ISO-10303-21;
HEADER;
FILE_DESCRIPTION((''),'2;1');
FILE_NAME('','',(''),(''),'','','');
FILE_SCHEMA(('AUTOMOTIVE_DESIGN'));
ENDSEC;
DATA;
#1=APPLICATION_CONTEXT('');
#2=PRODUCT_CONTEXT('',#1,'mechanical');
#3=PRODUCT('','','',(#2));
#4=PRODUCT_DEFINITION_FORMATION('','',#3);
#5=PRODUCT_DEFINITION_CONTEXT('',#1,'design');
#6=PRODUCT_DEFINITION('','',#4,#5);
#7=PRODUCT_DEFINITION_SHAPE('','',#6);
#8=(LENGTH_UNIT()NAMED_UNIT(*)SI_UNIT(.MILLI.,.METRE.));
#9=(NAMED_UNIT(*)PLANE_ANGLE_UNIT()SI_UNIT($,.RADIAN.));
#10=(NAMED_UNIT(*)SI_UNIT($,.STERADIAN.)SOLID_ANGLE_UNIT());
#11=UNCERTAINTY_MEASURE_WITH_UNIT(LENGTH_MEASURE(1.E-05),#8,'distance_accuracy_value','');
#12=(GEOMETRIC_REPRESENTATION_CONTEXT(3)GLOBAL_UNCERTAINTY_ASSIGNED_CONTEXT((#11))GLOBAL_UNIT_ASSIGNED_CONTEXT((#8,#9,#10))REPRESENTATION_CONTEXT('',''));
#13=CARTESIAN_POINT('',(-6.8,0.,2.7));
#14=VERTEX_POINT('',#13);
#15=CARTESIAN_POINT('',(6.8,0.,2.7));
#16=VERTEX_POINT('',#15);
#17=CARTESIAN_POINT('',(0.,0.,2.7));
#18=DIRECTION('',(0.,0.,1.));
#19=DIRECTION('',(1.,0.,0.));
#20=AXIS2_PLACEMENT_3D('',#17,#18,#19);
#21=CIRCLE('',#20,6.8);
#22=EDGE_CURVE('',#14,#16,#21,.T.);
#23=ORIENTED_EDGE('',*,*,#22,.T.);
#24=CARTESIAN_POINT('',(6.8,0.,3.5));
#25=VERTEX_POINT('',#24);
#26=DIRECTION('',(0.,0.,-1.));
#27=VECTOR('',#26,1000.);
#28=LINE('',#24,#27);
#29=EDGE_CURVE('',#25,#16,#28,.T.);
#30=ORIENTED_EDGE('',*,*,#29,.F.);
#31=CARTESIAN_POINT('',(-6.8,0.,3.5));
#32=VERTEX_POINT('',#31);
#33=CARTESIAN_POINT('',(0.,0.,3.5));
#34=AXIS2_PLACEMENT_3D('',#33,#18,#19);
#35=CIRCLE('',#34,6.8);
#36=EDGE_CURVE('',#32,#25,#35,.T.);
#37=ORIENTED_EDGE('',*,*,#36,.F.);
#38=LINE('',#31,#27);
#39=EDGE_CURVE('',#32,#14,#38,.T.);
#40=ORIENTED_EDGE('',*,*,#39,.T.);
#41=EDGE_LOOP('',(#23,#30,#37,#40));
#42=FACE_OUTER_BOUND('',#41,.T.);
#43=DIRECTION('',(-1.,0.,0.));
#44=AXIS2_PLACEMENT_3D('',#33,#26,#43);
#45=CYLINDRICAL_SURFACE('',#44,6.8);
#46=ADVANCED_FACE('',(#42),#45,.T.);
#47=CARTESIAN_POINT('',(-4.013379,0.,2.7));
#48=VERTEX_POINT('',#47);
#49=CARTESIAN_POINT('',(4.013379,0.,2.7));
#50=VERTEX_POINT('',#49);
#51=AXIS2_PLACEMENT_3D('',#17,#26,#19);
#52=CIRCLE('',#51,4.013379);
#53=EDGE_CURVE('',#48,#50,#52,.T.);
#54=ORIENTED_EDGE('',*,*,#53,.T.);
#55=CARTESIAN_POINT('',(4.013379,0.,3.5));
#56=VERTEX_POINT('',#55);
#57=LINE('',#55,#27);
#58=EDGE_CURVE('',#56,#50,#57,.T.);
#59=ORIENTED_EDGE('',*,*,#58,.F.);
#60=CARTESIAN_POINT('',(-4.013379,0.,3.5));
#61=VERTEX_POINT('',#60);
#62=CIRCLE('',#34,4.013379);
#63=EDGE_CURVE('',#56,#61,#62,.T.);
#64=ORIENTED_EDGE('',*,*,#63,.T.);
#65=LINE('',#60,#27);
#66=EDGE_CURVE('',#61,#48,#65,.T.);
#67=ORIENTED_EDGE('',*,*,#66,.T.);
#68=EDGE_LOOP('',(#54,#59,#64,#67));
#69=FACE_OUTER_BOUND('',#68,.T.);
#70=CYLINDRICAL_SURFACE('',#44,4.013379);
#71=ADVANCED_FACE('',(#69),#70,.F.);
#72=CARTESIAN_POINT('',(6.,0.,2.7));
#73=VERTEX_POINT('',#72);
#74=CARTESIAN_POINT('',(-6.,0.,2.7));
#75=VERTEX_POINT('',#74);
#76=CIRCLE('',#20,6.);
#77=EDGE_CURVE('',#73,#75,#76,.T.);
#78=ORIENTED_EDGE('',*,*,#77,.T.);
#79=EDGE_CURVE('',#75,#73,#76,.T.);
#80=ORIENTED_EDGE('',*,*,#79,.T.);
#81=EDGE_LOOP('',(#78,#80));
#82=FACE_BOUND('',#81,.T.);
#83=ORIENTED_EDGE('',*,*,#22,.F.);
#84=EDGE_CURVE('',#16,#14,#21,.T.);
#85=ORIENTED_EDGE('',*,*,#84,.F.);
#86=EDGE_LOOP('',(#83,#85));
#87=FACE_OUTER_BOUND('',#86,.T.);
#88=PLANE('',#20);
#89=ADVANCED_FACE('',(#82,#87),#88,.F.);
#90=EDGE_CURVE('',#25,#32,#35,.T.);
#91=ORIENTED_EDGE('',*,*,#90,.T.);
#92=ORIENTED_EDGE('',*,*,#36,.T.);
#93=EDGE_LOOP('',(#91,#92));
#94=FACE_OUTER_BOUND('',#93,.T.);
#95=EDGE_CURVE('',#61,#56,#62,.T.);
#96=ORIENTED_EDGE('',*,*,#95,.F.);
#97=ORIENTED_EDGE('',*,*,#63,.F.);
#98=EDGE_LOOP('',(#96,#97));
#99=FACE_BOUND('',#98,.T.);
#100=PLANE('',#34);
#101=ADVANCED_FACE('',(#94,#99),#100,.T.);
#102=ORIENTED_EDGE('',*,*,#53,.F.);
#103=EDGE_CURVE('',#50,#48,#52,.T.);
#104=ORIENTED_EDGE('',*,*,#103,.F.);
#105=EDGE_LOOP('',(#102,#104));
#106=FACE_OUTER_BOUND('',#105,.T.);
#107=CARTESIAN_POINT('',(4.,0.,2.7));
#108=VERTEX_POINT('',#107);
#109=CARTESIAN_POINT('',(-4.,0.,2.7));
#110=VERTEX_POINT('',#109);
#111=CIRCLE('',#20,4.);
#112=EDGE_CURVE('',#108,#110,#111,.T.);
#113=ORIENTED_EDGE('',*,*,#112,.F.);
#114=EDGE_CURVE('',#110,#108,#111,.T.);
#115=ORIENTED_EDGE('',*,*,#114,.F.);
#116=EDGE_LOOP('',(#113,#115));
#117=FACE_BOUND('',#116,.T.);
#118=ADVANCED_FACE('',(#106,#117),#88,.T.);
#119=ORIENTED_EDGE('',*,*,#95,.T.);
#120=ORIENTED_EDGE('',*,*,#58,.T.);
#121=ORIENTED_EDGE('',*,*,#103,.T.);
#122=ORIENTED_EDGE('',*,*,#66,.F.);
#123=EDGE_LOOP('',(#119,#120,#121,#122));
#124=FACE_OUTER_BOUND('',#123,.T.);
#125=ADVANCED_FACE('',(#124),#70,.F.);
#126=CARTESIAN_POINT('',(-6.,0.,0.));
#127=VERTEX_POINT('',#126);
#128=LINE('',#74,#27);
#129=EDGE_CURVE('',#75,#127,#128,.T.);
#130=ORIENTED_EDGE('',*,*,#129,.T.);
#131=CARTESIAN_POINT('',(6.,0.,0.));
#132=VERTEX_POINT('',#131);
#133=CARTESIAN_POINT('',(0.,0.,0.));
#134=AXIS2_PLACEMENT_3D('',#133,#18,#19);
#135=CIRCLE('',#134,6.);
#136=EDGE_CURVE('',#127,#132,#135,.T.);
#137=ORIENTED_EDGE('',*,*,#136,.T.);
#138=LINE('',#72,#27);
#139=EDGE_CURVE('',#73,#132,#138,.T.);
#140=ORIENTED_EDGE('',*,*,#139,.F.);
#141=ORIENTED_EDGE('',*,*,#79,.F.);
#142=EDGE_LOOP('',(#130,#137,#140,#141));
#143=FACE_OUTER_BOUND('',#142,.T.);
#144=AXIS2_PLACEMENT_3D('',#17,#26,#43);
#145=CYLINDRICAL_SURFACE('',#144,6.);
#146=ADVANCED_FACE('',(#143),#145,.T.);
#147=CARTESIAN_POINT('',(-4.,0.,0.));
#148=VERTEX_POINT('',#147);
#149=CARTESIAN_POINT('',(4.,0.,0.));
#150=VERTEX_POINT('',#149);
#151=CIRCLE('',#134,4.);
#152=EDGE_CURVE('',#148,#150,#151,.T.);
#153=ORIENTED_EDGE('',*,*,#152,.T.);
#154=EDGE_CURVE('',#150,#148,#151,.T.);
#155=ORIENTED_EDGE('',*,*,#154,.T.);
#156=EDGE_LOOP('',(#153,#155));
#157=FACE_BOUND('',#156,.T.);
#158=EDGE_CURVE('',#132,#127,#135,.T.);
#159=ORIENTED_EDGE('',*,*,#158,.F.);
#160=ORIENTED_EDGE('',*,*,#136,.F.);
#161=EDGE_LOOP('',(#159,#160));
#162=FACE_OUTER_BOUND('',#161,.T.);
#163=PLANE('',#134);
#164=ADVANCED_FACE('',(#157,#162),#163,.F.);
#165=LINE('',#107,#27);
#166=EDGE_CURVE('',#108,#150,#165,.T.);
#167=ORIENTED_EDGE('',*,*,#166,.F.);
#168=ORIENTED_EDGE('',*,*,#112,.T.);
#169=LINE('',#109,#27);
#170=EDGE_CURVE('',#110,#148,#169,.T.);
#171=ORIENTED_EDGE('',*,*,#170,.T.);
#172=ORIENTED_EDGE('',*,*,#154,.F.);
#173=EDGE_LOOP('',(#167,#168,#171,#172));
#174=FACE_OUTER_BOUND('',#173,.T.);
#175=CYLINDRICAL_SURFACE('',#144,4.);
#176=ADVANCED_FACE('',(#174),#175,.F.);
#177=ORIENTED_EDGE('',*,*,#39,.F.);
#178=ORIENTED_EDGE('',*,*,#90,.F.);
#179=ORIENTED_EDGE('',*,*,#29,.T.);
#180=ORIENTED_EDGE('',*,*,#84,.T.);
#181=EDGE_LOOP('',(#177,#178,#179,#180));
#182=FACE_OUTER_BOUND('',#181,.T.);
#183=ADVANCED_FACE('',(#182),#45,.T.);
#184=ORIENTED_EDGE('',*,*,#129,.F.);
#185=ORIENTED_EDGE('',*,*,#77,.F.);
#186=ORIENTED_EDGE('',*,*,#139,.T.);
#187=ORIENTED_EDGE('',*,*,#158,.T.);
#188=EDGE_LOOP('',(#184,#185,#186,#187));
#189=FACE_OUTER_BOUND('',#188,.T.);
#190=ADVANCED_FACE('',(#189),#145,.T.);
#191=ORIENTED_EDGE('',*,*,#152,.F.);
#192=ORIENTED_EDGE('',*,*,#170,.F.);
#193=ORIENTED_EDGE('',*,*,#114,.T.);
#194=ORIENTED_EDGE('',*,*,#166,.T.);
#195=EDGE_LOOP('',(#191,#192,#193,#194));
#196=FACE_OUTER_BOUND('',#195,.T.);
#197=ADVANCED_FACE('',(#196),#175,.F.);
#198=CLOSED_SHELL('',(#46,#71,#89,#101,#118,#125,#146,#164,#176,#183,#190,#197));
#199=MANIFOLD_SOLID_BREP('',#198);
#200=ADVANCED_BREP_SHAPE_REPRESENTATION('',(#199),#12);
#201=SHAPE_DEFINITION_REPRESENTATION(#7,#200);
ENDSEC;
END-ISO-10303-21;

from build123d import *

# Parameters (mm, degrees)
SKETCH_1_R      = 6
SKETCH_1_R_2    = 4
EXTRUDE_1_DEPTH = 2.7
SKETCH_2_R      = 6.8
SKETCH_2_R_2    = 4.013379479
EXTRUDE_2_DEPTH = 0.8


with BuildPart() as part:
    # 草图1 → 凸台-拉伸1 (new body)
    with BuildSketch(Plane.XY):
        with Locations(Location((0, 0, 0), (0, 0, 180))):
            Circle(SKETCH_1_R)
        with Locations(Location((0, 0, 0), (0, 0, 180))):
            Circle(SKETCH_1_R_2, mode=Mode.SUBTRACT)
    extrude(amount=EXTRUDE_1_DEPTH)

    # 草图2 → 凸台-拉伸2 (add)
    with BuildSketch(Plane.XY.offset(2.7)):
        Circle(SKETCH_2_R)
        Circle(SKETCH_2_R_2, mode=Mode.SUBTRACT)
    extrude(amount=EXTRUDE_2_DEPTH)


solid = part.part
